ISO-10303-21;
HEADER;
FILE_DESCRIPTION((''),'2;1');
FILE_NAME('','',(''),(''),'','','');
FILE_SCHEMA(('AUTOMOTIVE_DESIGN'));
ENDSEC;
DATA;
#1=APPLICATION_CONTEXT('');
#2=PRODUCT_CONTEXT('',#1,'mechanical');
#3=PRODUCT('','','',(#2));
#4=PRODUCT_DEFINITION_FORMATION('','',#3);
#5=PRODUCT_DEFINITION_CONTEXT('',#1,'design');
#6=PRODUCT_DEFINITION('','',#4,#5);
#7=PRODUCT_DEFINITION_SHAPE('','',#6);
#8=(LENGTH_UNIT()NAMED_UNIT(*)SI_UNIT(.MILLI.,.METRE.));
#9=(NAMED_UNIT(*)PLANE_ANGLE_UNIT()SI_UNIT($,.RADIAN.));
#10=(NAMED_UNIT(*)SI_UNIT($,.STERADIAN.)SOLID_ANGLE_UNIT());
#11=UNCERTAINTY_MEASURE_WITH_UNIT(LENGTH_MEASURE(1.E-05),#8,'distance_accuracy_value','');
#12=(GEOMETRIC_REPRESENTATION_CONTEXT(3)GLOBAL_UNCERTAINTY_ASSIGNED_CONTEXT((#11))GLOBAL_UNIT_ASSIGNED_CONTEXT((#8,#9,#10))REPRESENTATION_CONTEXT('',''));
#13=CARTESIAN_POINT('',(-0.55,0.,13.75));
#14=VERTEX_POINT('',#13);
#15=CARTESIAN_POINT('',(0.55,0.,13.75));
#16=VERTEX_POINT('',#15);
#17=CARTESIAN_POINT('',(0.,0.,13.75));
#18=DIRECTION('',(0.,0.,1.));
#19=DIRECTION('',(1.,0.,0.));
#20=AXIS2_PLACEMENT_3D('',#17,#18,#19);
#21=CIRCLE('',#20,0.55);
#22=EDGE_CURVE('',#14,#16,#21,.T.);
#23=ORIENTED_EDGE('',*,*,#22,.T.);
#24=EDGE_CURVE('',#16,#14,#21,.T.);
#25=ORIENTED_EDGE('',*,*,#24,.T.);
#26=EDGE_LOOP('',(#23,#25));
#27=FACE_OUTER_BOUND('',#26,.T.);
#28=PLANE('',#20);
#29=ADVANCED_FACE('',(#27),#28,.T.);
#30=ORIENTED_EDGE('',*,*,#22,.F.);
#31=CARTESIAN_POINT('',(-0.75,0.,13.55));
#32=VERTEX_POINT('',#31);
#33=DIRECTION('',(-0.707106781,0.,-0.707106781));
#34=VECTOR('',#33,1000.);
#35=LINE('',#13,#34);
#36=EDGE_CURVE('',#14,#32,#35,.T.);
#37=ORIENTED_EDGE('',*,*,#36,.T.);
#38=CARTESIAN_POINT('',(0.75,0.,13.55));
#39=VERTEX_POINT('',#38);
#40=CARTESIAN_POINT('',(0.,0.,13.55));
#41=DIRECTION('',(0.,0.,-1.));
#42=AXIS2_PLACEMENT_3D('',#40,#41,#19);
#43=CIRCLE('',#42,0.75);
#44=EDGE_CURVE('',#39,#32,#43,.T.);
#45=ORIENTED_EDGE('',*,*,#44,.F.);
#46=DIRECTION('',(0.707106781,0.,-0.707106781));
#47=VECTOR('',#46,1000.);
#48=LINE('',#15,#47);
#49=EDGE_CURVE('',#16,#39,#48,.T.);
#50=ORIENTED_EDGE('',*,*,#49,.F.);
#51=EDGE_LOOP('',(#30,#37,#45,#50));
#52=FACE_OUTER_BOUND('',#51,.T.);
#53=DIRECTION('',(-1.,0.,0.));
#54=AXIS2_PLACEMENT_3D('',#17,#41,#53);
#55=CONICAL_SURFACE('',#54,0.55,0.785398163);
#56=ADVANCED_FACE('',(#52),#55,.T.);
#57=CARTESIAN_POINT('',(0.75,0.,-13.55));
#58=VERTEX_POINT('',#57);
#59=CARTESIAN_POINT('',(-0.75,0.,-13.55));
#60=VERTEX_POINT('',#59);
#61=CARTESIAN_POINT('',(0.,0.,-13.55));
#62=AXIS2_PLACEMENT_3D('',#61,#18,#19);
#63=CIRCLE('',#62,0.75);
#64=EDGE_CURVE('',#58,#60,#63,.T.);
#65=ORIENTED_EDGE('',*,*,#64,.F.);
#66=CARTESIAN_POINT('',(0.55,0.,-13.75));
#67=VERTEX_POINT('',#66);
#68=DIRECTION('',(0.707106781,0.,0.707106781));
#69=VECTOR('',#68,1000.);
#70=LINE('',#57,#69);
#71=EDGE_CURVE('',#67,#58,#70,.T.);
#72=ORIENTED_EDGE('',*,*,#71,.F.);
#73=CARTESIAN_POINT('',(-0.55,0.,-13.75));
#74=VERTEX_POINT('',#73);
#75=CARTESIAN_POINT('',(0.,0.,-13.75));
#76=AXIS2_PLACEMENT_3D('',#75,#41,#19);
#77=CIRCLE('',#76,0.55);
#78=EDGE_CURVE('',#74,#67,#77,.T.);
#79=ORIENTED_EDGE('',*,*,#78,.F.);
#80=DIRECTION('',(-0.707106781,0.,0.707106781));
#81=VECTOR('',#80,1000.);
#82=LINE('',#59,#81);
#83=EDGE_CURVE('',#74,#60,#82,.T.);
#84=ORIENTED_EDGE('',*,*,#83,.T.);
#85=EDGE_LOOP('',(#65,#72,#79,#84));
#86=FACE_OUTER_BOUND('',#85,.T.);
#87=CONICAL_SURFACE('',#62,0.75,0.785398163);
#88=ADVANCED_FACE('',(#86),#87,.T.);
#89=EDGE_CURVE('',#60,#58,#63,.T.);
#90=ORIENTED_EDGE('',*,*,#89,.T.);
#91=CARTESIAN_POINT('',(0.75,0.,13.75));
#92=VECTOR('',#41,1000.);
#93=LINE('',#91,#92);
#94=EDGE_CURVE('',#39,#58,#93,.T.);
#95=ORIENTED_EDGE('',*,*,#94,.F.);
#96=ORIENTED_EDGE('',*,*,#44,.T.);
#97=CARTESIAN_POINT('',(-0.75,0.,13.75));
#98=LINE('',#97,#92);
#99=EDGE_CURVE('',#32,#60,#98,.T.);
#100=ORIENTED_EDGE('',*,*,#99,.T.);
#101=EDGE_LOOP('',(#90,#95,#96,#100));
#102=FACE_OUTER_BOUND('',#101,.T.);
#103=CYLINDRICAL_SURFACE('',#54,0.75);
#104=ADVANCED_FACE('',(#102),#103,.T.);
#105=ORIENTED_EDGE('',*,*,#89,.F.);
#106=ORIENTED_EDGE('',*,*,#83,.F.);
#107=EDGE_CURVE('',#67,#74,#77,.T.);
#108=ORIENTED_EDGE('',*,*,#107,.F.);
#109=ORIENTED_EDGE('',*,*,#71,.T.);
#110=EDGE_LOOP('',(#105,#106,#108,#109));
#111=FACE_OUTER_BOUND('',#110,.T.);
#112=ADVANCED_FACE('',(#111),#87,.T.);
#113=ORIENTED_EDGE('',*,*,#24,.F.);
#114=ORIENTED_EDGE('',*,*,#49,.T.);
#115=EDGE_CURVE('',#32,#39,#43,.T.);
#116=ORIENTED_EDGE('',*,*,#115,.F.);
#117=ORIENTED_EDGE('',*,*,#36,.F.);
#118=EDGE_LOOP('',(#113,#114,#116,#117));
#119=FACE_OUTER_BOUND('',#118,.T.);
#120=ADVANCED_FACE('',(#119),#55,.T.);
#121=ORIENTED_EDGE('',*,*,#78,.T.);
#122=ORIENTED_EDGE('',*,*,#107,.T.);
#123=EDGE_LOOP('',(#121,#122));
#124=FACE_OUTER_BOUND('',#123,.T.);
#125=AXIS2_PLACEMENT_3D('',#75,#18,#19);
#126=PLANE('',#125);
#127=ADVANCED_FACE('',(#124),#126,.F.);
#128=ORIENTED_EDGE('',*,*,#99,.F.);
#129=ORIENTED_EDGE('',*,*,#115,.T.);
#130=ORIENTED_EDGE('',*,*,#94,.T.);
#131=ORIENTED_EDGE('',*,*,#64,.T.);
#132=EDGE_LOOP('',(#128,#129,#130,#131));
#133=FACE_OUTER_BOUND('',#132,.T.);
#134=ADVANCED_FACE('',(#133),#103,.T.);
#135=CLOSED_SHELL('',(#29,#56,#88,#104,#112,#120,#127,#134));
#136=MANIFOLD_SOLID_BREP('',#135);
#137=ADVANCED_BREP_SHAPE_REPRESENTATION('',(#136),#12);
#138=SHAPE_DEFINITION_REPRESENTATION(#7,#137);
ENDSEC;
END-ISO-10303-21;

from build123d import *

# Parameters (mm, degrees)
SKETCH1_R           = 0.75
BOSS_EXTRUDE1_DEPTH = 13.75
CHAMFER1_SIZE       = 0.2


with BuildPart() as part:
    # Sketch1 → Boss-Extrude1 (new, symmetric)
    with BuildSketch(Plane.XY):
        Circle(SKETCH1_R)
    extrude(amount=BOSS_EXTRUDE1_DEPTH, both=True)

    # Chamfer1
    chamfer1_edges = [part.edges().sort_by_distance(p)[0] for p in [
        (-0.75, 0, -13.75),
        (-0.75, 0, 13.75),
    ]]
    chamfer(chamfer1_edges, length=CHAMFER1_SIZE)


solid = part.part
